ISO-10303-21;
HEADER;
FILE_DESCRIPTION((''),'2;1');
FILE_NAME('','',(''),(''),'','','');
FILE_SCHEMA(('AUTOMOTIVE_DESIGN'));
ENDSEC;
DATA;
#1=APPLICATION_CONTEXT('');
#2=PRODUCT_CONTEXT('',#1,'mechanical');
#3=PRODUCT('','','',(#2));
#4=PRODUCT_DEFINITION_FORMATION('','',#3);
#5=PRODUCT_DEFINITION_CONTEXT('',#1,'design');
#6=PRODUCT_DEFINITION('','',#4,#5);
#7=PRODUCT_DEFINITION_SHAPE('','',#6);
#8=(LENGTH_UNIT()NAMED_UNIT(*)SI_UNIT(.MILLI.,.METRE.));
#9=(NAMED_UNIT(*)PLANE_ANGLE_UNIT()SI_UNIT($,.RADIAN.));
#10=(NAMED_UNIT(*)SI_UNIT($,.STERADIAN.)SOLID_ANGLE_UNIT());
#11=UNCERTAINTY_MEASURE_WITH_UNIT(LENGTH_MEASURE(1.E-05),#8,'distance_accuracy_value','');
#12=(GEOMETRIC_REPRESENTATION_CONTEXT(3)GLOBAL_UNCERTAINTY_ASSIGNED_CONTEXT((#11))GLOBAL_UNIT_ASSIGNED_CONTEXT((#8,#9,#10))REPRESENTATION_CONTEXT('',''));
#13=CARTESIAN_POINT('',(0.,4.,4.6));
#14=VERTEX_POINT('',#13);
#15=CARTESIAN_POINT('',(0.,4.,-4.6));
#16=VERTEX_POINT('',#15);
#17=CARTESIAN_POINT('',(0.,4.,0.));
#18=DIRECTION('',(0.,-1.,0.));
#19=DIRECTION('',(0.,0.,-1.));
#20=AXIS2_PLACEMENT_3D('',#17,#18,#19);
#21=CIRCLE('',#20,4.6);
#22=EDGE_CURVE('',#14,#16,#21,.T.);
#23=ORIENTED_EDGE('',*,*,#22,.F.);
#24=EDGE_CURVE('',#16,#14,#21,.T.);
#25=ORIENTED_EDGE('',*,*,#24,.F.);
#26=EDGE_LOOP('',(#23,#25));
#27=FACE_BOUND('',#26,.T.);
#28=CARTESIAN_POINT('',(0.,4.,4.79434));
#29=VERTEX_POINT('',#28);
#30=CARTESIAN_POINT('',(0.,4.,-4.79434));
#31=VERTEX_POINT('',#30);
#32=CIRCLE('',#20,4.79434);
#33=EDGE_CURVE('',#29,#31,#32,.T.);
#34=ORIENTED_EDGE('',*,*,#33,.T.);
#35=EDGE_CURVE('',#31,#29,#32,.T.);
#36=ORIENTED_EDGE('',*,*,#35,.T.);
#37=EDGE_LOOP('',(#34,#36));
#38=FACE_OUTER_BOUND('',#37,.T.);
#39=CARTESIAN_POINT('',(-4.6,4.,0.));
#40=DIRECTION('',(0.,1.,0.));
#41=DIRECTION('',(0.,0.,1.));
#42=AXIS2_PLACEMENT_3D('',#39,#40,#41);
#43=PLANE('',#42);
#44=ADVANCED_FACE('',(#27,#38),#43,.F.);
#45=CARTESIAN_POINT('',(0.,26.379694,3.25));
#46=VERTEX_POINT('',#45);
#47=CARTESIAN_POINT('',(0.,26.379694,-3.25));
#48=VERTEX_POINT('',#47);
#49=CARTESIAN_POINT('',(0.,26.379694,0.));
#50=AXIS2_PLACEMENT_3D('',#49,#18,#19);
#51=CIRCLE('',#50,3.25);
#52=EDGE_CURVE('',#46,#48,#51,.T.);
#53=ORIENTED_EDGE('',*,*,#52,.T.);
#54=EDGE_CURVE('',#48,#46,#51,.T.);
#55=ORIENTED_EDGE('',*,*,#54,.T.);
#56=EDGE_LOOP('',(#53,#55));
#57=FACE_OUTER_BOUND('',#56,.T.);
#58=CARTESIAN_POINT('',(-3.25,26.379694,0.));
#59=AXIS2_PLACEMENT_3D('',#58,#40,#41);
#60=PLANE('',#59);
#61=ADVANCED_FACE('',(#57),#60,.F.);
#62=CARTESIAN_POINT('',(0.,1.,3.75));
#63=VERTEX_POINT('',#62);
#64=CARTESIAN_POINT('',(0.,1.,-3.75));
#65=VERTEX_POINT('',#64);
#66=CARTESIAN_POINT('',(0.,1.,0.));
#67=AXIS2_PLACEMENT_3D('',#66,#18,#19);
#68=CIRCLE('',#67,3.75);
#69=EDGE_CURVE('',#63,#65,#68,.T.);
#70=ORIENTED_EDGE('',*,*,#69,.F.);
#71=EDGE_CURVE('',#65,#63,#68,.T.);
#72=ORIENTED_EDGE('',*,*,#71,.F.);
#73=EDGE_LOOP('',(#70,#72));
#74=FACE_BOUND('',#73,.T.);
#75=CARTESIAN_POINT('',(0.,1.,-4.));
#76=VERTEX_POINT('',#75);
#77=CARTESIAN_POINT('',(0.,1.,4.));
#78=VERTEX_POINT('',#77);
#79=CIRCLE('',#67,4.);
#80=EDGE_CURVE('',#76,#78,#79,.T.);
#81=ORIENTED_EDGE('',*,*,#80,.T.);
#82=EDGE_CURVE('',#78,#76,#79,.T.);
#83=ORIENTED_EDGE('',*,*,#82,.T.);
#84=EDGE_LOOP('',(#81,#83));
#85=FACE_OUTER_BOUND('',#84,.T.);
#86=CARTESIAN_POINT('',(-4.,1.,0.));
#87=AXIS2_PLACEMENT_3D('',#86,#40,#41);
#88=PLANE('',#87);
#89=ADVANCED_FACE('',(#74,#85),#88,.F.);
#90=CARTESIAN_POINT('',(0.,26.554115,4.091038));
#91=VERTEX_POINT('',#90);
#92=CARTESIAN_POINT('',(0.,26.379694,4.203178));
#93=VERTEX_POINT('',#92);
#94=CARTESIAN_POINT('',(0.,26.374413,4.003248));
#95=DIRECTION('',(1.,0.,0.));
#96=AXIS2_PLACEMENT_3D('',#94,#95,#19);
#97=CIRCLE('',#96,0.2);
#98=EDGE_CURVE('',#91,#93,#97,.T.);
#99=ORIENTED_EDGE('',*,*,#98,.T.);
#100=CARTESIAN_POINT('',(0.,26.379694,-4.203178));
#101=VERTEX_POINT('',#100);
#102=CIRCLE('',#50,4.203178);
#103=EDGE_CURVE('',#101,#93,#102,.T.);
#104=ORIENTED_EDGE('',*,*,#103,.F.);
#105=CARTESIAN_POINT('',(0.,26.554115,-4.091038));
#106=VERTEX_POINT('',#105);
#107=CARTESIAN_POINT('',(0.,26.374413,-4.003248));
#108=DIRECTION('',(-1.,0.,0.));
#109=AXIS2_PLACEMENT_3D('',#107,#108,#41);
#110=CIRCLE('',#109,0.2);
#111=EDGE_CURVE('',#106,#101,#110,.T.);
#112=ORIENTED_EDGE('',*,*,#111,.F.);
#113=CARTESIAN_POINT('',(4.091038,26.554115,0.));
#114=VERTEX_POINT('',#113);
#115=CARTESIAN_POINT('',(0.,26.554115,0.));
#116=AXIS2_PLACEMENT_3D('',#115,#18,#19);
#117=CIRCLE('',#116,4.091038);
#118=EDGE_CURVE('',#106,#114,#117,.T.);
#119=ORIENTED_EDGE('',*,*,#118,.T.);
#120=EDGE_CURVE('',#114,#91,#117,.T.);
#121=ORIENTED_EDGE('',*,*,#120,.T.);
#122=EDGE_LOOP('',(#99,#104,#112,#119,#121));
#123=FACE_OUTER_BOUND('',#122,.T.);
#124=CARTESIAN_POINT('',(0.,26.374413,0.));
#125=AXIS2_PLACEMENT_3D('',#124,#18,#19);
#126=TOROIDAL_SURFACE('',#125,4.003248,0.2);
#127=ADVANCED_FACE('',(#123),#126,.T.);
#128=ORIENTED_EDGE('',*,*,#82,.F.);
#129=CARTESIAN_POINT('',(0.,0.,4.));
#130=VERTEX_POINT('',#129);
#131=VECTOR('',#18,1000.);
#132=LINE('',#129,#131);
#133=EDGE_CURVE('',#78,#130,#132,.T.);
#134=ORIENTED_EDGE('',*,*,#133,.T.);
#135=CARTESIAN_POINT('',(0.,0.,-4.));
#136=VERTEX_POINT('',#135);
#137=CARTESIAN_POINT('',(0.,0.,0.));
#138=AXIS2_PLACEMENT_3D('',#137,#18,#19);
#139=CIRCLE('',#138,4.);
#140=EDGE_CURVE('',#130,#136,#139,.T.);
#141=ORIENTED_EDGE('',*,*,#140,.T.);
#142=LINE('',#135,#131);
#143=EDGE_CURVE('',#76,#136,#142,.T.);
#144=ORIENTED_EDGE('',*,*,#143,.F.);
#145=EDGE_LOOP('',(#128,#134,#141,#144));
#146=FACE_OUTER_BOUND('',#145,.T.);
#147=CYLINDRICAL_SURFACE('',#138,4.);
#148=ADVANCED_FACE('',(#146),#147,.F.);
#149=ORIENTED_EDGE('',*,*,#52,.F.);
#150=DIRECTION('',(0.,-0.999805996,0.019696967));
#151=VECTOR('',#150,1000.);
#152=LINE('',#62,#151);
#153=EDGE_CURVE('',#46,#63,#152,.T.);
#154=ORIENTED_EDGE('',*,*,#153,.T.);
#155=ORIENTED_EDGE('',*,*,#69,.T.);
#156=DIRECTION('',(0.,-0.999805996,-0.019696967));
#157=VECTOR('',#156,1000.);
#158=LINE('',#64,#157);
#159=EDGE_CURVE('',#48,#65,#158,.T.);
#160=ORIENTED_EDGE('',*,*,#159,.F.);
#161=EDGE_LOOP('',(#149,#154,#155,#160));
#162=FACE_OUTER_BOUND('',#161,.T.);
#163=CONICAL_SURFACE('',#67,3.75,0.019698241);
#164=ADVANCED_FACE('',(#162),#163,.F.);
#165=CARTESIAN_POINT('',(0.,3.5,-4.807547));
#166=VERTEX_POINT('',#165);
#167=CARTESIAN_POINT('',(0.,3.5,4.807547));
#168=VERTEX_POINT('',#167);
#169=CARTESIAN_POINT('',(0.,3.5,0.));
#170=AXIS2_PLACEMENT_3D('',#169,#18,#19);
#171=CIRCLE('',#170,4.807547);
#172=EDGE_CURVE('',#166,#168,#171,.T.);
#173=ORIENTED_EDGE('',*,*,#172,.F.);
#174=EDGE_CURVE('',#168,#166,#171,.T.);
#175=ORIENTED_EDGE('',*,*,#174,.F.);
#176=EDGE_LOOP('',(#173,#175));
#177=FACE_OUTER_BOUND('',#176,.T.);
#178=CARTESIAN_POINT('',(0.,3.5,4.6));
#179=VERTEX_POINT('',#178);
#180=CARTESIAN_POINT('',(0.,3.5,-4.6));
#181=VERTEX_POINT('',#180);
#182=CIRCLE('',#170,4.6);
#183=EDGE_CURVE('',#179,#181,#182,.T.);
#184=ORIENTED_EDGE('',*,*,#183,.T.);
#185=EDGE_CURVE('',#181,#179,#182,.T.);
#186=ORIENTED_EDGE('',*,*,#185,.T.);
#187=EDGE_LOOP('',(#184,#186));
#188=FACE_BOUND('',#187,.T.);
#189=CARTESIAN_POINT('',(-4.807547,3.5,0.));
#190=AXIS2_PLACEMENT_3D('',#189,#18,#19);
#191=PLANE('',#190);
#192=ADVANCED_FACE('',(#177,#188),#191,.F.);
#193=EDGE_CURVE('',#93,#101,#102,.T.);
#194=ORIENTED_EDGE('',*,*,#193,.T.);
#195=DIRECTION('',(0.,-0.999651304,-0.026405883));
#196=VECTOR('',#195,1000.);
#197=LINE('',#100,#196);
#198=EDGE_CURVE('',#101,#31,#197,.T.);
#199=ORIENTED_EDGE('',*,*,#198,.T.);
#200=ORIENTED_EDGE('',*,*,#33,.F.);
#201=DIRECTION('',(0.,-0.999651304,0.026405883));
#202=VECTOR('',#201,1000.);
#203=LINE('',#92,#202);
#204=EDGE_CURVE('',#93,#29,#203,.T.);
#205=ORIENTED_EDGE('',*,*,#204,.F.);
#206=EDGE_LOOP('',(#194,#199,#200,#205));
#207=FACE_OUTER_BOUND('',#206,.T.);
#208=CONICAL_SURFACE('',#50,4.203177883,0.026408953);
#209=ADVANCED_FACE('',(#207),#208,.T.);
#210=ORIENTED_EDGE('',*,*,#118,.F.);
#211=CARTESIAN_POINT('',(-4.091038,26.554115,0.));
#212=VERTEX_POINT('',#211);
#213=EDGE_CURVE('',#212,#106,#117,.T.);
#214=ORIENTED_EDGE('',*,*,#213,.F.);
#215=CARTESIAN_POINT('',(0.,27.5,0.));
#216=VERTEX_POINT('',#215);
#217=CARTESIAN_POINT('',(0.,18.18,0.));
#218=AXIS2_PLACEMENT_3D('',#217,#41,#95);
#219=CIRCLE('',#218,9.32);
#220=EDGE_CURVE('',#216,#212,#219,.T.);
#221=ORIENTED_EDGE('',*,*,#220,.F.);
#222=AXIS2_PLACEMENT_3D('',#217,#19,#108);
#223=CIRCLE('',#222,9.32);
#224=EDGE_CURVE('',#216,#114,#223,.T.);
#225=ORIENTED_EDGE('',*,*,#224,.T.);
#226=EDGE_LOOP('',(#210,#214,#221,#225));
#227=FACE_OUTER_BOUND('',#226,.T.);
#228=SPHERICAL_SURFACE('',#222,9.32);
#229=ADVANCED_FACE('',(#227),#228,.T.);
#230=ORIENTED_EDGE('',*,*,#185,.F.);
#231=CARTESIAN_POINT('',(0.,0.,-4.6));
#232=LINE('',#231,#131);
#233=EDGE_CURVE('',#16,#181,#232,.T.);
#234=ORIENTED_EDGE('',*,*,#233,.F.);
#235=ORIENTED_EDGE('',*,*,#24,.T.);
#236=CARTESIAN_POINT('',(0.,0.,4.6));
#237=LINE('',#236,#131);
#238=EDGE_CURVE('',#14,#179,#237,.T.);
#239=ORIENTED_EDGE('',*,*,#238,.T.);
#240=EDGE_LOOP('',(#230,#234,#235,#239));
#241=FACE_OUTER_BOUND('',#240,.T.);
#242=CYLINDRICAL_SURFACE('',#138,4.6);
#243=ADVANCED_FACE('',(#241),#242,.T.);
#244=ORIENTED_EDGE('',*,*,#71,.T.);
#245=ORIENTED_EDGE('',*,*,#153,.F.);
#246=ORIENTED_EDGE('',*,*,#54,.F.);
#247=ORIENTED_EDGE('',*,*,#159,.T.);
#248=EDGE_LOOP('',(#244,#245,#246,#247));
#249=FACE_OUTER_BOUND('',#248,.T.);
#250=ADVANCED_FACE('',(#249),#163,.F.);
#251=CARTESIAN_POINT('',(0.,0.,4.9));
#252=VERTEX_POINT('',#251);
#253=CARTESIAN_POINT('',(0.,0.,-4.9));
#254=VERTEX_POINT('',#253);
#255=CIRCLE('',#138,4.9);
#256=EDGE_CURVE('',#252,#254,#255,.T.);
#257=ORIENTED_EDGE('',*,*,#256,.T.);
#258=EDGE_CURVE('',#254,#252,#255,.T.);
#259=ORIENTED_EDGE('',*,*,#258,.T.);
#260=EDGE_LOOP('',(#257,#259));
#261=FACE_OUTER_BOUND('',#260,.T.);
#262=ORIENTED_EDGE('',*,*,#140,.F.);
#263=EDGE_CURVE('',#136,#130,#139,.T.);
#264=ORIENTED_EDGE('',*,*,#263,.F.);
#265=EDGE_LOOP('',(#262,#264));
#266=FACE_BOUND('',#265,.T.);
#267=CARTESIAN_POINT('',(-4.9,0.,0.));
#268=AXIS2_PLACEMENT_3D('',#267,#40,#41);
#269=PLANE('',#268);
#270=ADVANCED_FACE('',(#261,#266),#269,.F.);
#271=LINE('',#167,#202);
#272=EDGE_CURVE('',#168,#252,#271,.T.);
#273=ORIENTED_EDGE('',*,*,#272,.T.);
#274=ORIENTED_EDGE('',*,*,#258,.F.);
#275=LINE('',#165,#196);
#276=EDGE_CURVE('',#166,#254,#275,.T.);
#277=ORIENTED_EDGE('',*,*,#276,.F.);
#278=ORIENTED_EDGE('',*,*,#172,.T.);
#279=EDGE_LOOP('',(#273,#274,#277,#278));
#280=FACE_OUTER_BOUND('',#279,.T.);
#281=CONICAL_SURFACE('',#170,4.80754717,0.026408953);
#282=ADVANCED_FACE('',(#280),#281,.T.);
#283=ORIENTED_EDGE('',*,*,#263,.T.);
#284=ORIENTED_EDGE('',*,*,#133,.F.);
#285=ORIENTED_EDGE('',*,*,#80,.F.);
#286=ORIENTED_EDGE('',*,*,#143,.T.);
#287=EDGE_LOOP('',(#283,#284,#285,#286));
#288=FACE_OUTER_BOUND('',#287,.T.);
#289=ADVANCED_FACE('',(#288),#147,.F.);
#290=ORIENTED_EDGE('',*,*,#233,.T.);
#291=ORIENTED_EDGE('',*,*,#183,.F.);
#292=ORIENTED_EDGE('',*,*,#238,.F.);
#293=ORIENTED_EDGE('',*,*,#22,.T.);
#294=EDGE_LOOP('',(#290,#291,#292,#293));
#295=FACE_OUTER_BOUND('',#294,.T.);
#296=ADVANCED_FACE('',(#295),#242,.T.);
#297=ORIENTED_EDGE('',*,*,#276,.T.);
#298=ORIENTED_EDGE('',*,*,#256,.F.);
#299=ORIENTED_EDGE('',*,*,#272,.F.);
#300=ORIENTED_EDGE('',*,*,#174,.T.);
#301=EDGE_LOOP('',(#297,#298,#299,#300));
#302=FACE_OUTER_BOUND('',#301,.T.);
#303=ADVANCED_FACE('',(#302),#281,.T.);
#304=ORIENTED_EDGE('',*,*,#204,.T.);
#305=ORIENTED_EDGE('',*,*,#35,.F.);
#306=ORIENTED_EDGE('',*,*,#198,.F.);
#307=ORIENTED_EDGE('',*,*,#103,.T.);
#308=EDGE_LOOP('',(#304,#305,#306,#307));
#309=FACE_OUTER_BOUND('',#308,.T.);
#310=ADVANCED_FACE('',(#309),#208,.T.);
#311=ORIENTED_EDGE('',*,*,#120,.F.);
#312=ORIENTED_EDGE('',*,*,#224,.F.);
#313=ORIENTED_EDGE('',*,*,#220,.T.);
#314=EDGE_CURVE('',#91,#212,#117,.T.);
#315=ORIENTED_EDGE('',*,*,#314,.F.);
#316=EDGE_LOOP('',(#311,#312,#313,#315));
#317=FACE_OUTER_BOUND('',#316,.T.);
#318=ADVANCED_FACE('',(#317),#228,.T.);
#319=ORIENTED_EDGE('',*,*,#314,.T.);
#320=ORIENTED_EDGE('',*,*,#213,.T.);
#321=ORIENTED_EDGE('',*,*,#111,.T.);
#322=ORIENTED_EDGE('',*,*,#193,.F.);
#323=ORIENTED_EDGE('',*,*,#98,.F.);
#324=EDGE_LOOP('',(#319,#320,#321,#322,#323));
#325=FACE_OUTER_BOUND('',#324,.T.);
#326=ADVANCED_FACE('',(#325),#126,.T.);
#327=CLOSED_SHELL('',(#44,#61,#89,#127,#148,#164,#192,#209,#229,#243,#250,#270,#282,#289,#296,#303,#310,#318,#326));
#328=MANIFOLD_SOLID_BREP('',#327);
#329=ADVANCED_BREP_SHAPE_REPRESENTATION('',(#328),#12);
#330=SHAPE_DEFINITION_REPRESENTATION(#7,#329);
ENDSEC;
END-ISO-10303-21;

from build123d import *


with BuildPart() as part:
    # Sketch1 → Revolve1 (revolve)
    with BuildSketch(Plane.XY, mode=Mode.PRIVATE) as revolve1_sk:
        with BuildLine():
            Line((-4.9, 0), (-4.80754717, 3.5))
            Line((-4.80754717, 3.5), (-4.6, 3.5))
            Line((-4.6, 3.5), (-4.6, 4))
            Line((-4.6, 4), (-4.794339623, 4))
            Line((-4.794339623, 4), (-4.203177883, 26.379694424))
            ThreePointArc((-4.203177883, 26.379694424), (-4.171478034, 26.482572984), (-4.09103814, 26.554115293))
            ThreePointArc((-4.09103814, 26.554115293), (-2.09948154, 27.260450279), (0, 27.5))
            Line((0, 27.5), (0, 26.379694424))
            Line((0, 26.379694424), (-3.25, 26.379694424))
            Line((-3.25, 26.379694424), (-3.75, 1))
            Line((-3.75, 1), (-4, 1))
            Line((-4, 1), (-4, 0))
            Line((-4, 0), (-4.9, 0))
        make_face()
    revolve(revolve1_sk.sketch.rotate(Axis((0, 0, 0), (0, 1, 0)), 270), axis=Axis((0, 0, 0), (0, 1, 0)))


solid = part.part
